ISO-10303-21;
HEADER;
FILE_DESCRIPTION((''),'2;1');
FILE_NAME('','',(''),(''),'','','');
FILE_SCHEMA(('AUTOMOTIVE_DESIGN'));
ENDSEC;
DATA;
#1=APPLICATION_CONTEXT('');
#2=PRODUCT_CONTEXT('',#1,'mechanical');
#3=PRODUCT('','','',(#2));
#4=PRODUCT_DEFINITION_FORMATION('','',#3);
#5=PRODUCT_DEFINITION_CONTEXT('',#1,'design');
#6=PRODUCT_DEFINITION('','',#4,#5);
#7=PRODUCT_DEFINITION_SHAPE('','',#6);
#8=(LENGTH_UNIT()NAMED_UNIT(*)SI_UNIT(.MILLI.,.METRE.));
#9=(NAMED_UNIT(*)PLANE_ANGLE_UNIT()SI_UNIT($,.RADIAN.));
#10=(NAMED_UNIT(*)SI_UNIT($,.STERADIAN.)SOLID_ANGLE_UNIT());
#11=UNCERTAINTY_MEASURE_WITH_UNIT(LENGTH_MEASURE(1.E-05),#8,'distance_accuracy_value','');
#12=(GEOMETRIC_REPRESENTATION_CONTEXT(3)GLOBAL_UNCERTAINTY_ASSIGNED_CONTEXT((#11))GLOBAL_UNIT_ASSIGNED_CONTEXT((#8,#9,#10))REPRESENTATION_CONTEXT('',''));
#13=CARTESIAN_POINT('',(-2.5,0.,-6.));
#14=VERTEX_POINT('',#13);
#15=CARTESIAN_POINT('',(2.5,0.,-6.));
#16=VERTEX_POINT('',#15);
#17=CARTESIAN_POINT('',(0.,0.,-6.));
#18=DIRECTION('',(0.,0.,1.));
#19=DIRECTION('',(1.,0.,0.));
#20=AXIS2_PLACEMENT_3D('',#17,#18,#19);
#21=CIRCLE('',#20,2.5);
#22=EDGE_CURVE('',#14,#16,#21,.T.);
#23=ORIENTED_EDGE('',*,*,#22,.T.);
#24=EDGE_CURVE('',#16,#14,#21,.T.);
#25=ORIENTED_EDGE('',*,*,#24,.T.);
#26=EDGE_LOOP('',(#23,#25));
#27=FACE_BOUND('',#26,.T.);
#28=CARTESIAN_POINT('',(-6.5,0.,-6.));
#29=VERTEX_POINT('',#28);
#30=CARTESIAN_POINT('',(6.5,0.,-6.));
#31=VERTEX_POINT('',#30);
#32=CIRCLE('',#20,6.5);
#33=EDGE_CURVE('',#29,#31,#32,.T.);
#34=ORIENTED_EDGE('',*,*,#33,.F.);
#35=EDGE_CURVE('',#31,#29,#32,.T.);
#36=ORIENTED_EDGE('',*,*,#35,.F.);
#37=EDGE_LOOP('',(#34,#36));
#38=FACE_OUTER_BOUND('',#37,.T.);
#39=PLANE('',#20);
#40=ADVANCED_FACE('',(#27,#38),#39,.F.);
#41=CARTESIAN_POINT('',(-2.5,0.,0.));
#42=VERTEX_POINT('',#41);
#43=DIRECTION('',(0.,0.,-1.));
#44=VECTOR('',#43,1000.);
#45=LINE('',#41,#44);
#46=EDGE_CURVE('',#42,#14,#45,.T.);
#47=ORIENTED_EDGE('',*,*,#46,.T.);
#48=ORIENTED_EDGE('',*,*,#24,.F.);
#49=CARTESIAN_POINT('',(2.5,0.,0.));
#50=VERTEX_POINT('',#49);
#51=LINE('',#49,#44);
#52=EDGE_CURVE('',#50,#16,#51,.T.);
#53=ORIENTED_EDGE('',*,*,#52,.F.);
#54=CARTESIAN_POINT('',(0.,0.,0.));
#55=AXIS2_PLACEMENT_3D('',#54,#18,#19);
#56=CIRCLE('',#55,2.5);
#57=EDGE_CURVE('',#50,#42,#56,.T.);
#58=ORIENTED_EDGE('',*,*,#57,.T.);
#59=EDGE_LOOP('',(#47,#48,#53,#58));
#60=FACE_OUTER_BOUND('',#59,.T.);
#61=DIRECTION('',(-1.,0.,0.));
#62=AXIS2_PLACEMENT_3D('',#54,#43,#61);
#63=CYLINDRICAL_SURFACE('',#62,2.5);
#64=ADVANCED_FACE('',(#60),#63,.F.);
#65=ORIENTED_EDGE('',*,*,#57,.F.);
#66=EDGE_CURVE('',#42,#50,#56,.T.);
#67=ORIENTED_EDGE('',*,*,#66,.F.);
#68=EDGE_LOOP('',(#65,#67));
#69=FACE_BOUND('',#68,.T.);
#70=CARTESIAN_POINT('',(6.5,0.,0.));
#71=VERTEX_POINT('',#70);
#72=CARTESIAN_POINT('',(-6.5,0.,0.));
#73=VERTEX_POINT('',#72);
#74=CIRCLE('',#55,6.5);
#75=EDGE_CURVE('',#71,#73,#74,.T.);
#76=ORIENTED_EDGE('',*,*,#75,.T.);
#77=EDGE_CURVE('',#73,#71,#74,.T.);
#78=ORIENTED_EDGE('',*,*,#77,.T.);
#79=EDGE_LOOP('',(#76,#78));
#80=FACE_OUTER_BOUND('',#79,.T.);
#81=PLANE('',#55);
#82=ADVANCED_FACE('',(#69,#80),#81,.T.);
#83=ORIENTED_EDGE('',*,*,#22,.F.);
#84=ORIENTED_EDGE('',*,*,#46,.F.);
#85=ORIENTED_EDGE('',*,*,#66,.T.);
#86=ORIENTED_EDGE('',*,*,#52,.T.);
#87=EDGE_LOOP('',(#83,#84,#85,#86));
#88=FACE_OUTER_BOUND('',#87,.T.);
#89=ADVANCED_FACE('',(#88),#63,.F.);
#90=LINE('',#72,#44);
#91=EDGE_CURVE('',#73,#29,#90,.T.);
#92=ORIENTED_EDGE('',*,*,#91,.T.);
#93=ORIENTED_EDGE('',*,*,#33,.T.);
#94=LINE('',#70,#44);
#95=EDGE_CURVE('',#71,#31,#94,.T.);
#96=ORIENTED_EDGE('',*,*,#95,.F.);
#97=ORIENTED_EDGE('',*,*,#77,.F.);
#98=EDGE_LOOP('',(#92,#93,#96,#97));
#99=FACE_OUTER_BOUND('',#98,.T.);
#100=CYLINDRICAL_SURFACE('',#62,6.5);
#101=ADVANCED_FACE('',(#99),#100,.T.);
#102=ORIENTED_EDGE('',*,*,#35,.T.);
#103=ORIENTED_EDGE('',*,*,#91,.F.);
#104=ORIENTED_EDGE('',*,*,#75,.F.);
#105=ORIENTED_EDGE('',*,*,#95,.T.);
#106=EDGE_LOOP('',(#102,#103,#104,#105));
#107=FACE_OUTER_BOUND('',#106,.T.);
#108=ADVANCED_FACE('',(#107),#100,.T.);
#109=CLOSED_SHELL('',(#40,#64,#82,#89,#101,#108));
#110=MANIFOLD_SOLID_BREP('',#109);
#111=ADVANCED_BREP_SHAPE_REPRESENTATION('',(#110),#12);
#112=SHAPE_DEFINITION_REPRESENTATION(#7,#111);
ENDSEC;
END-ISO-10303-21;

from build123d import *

# Parameters (mm, degrees)
SKETCH1_R           = 6.5
SKETCH1_R_2         = 2.5
BOSS_EXTRUDE1_DEPTH = 6


with BuildPart() as part:
    # Sketch1 → Boss-Extrude1 (new body)
    with BuildSketch(Plane.XY.offset(-6)):
        Circle(SKETCH1_R)
        Circle(SKETCH1_R_2, mode=Mode.SUBTRACT)
    extrude(amount=BOSS_EXTRUDE1_DEPTH)


solid = part.part
